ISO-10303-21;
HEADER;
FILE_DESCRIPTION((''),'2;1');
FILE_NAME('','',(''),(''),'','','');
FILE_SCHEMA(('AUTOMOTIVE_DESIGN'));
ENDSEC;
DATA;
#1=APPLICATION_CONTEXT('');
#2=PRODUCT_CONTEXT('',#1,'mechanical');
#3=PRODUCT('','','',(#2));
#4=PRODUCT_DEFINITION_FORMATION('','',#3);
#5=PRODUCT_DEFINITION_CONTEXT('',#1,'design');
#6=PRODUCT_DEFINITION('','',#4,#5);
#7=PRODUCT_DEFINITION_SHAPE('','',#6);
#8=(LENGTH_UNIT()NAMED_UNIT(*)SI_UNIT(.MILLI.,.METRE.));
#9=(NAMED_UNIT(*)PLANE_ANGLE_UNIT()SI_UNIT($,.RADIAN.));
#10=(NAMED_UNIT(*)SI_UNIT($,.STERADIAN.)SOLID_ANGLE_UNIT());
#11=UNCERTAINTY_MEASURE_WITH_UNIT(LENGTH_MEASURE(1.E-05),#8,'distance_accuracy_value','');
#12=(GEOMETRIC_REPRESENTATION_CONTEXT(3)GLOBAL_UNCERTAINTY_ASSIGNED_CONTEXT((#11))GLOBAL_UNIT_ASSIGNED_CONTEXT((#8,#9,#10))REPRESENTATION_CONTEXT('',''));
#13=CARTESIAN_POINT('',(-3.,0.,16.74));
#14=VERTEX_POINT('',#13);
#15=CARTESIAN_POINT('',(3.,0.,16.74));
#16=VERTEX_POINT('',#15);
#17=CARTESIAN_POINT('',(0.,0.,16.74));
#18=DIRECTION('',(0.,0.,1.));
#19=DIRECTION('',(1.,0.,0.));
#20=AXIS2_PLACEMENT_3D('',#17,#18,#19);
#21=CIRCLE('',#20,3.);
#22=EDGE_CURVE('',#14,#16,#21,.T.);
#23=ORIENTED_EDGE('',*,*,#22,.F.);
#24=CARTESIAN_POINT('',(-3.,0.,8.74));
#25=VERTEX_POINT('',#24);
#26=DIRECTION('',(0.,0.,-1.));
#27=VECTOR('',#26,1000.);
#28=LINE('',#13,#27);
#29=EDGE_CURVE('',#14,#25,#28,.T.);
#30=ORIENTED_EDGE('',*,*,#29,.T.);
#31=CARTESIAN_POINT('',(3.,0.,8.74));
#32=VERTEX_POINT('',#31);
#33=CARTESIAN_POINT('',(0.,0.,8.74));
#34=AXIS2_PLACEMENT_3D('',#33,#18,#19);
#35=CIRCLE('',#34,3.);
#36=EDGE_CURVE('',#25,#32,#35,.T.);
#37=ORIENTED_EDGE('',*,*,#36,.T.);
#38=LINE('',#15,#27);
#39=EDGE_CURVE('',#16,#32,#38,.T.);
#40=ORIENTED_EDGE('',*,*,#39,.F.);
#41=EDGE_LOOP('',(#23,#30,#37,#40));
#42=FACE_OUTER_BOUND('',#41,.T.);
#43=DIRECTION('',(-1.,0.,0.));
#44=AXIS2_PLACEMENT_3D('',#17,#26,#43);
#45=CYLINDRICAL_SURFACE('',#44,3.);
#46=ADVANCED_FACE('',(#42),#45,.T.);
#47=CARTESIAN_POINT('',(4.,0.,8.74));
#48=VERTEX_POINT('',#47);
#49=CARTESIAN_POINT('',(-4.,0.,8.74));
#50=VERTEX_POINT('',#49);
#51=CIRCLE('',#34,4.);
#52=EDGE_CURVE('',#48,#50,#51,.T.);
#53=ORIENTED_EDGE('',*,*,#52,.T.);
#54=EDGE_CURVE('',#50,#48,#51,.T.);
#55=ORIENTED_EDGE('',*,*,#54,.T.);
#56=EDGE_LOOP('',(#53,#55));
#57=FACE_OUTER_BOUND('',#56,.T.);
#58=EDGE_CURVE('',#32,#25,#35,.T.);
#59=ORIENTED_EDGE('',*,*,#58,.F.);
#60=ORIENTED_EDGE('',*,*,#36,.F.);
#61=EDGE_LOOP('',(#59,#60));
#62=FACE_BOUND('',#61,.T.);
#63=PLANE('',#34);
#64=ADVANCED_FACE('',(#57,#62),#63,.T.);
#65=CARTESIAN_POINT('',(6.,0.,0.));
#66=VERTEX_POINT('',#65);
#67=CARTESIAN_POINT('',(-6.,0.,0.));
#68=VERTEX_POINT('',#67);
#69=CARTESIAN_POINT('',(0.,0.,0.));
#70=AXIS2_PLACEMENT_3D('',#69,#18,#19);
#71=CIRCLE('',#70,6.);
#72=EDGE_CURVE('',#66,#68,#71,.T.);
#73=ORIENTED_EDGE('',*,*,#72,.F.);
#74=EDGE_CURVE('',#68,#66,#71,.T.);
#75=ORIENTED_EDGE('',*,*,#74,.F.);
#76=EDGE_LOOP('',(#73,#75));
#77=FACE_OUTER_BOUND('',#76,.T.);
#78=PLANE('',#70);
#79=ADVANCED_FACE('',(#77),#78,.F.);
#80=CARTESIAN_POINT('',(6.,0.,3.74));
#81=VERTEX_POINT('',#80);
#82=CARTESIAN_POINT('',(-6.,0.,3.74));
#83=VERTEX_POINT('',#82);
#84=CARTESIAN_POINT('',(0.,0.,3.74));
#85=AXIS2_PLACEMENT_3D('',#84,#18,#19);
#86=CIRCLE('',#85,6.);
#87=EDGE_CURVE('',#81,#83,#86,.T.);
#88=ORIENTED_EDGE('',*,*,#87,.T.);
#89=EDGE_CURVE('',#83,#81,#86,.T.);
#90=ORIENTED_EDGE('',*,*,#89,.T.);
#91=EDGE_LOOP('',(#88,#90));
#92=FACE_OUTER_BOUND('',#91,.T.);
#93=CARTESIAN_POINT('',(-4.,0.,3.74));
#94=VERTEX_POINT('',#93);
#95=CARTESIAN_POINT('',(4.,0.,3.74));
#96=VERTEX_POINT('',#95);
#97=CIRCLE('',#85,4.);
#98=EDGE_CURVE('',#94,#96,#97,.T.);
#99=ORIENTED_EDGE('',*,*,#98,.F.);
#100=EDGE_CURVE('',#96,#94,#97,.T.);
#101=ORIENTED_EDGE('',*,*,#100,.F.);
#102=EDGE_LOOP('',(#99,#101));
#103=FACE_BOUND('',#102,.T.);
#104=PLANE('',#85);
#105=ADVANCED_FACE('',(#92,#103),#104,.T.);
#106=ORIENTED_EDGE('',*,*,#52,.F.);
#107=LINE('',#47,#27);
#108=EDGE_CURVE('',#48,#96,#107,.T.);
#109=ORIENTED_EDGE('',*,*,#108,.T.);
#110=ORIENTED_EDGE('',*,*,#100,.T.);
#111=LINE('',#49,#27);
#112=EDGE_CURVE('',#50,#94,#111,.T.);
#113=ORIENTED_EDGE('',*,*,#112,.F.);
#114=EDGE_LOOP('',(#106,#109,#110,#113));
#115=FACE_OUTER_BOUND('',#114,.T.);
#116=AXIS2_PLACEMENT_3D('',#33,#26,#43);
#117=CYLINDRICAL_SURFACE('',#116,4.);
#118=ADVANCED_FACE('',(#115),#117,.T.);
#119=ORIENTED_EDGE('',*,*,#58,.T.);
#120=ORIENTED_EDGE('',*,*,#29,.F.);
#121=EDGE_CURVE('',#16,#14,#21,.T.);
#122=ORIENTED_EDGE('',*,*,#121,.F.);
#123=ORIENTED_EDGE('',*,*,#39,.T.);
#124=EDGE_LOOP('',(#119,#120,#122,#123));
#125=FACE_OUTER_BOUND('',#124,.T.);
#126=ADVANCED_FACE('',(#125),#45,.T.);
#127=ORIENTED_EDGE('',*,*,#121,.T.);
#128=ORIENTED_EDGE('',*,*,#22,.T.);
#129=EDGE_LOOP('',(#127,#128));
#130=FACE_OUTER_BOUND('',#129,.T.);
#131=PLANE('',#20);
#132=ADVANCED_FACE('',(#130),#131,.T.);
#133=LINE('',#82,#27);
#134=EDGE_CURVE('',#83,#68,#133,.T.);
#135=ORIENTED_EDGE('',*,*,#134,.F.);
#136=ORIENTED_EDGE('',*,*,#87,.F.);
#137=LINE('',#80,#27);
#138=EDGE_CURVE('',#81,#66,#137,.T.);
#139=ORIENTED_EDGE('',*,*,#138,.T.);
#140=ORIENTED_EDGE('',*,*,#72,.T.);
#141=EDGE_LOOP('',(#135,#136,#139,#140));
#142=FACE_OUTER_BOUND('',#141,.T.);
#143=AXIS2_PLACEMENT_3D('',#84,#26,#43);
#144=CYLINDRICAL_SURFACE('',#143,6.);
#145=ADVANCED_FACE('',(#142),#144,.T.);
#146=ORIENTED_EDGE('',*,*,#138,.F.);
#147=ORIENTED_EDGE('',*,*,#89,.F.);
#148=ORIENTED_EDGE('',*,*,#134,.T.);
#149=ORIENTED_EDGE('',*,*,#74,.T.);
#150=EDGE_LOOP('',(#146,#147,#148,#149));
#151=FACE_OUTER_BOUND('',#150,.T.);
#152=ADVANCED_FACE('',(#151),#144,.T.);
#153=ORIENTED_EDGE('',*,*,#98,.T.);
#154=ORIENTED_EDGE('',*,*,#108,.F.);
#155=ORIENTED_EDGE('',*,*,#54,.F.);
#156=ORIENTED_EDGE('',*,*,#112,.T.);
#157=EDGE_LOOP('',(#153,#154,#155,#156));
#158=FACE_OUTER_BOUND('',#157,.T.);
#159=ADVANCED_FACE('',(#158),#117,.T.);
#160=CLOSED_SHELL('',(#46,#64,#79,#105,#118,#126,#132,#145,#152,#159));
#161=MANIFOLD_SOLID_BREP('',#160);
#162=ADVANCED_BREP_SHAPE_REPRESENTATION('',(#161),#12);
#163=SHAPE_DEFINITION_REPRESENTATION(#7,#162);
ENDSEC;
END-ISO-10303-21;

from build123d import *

# Parameters (mm, degrees)
SKETCH_1_R      = 6
EXTRUDE_1_DEPTH = 3.74
SKETCH_2_R      = 4
EXTRUDE_2_DEPTH = 5
SKETCH_3_R      = 3
EXTRUDE_3_DEPTH = 8


with BuildPart() as part:
    # 草图1 → 凸台-拉伸1 (new body)
    with BuildSketch(Plane.XY):
        Circle(SKETCH_1_R)
    extrude(amount=EXTRUDE_1_DEPTH)

    # 草图2 → 凸台-拉伸2 (add)
    with BuildSketch(Plane.XY.offset(3.74)):
        Circle(SKETCH_2_R)
    extrude(amount=EXTRUDE_2_DEPTH)

    # 草图3 → 凸台-拉伸3 (add)
    with BuildSketch(Plane.XY.offset(8.74)):
        Circle(SKETCH_3_R)
    extrude(amount=EXTRUDE_3_DEPTH)


solid = part.part
